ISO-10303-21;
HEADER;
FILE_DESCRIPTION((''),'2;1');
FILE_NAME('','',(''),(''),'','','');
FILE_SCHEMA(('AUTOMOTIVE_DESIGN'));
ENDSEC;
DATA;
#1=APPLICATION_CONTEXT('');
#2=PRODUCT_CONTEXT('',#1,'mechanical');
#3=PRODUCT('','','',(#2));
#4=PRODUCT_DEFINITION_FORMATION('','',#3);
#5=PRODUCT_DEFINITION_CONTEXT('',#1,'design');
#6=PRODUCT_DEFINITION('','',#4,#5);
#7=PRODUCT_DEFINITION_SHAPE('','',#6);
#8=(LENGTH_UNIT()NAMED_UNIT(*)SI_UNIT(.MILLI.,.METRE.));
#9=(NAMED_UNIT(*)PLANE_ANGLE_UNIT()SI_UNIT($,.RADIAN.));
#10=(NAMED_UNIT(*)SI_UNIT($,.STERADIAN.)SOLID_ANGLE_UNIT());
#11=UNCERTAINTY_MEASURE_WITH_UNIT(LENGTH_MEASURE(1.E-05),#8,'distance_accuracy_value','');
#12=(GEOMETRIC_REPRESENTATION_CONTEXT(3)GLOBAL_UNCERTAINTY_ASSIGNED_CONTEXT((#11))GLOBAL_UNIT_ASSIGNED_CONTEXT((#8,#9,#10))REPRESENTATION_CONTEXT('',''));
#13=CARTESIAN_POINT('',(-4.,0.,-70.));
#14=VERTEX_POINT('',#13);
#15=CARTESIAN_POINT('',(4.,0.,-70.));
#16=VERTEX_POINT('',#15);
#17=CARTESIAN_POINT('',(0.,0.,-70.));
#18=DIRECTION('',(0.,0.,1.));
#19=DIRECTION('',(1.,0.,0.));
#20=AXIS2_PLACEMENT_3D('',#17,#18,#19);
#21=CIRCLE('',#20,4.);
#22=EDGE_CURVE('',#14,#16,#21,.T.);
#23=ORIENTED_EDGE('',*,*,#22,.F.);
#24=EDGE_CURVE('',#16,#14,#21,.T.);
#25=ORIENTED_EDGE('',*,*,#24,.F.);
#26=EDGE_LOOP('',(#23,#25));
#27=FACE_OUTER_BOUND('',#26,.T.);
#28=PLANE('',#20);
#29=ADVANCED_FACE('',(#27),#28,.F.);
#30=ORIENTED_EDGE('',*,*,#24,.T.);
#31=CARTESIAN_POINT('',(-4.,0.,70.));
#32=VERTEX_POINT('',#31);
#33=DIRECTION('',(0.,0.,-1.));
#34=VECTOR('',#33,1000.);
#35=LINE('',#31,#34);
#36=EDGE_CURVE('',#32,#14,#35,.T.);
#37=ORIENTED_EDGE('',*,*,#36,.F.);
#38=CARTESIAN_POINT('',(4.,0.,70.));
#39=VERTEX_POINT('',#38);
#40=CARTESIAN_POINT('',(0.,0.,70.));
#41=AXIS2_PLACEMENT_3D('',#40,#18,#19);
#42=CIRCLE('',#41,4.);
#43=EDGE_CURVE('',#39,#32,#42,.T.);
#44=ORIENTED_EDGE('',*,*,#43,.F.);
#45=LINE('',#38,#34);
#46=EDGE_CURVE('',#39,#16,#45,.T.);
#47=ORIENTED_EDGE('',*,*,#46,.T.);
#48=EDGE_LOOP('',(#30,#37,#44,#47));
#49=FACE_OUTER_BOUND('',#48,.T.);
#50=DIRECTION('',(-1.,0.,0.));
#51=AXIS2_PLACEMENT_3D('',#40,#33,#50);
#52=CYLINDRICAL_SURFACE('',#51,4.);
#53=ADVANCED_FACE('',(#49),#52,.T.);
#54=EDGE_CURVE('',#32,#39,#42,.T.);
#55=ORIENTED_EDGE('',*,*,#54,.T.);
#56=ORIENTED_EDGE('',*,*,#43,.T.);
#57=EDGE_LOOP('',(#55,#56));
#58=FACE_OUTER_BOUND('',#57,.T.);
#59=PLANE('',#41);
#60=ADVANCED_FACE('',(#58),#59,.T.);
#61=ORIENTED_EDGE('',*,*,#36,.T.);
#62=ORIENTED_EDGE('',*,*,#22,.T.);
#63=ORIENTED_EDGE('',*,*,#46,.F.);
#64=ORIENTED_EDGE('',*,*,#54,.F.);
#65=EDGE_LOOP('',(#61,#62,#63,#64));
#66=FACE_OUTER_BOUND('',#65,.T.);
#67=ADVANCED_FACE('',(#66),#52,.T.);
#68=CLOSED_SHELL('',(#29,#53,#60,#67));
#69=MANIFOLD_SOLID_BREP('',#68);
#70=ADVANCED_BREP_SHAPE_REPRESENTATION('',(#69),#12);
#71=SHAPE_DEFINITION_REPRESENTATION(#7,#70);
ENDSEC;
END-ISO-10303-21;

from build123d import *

# Parameters (mm, degrees)
SKETCH_1_R      = 4
EXTRUDE_1_DEPTH = 70


with BuildPart() as part:
    # 草图1 → 凸台-拉伸1 (new, symmetric)
    with BuildSketch(Plane.XY):
        Circle(SKETCH_1_R)
    extrude(amount=EXTRUDE_1_DEPTH, both=True)


solid = part.part
